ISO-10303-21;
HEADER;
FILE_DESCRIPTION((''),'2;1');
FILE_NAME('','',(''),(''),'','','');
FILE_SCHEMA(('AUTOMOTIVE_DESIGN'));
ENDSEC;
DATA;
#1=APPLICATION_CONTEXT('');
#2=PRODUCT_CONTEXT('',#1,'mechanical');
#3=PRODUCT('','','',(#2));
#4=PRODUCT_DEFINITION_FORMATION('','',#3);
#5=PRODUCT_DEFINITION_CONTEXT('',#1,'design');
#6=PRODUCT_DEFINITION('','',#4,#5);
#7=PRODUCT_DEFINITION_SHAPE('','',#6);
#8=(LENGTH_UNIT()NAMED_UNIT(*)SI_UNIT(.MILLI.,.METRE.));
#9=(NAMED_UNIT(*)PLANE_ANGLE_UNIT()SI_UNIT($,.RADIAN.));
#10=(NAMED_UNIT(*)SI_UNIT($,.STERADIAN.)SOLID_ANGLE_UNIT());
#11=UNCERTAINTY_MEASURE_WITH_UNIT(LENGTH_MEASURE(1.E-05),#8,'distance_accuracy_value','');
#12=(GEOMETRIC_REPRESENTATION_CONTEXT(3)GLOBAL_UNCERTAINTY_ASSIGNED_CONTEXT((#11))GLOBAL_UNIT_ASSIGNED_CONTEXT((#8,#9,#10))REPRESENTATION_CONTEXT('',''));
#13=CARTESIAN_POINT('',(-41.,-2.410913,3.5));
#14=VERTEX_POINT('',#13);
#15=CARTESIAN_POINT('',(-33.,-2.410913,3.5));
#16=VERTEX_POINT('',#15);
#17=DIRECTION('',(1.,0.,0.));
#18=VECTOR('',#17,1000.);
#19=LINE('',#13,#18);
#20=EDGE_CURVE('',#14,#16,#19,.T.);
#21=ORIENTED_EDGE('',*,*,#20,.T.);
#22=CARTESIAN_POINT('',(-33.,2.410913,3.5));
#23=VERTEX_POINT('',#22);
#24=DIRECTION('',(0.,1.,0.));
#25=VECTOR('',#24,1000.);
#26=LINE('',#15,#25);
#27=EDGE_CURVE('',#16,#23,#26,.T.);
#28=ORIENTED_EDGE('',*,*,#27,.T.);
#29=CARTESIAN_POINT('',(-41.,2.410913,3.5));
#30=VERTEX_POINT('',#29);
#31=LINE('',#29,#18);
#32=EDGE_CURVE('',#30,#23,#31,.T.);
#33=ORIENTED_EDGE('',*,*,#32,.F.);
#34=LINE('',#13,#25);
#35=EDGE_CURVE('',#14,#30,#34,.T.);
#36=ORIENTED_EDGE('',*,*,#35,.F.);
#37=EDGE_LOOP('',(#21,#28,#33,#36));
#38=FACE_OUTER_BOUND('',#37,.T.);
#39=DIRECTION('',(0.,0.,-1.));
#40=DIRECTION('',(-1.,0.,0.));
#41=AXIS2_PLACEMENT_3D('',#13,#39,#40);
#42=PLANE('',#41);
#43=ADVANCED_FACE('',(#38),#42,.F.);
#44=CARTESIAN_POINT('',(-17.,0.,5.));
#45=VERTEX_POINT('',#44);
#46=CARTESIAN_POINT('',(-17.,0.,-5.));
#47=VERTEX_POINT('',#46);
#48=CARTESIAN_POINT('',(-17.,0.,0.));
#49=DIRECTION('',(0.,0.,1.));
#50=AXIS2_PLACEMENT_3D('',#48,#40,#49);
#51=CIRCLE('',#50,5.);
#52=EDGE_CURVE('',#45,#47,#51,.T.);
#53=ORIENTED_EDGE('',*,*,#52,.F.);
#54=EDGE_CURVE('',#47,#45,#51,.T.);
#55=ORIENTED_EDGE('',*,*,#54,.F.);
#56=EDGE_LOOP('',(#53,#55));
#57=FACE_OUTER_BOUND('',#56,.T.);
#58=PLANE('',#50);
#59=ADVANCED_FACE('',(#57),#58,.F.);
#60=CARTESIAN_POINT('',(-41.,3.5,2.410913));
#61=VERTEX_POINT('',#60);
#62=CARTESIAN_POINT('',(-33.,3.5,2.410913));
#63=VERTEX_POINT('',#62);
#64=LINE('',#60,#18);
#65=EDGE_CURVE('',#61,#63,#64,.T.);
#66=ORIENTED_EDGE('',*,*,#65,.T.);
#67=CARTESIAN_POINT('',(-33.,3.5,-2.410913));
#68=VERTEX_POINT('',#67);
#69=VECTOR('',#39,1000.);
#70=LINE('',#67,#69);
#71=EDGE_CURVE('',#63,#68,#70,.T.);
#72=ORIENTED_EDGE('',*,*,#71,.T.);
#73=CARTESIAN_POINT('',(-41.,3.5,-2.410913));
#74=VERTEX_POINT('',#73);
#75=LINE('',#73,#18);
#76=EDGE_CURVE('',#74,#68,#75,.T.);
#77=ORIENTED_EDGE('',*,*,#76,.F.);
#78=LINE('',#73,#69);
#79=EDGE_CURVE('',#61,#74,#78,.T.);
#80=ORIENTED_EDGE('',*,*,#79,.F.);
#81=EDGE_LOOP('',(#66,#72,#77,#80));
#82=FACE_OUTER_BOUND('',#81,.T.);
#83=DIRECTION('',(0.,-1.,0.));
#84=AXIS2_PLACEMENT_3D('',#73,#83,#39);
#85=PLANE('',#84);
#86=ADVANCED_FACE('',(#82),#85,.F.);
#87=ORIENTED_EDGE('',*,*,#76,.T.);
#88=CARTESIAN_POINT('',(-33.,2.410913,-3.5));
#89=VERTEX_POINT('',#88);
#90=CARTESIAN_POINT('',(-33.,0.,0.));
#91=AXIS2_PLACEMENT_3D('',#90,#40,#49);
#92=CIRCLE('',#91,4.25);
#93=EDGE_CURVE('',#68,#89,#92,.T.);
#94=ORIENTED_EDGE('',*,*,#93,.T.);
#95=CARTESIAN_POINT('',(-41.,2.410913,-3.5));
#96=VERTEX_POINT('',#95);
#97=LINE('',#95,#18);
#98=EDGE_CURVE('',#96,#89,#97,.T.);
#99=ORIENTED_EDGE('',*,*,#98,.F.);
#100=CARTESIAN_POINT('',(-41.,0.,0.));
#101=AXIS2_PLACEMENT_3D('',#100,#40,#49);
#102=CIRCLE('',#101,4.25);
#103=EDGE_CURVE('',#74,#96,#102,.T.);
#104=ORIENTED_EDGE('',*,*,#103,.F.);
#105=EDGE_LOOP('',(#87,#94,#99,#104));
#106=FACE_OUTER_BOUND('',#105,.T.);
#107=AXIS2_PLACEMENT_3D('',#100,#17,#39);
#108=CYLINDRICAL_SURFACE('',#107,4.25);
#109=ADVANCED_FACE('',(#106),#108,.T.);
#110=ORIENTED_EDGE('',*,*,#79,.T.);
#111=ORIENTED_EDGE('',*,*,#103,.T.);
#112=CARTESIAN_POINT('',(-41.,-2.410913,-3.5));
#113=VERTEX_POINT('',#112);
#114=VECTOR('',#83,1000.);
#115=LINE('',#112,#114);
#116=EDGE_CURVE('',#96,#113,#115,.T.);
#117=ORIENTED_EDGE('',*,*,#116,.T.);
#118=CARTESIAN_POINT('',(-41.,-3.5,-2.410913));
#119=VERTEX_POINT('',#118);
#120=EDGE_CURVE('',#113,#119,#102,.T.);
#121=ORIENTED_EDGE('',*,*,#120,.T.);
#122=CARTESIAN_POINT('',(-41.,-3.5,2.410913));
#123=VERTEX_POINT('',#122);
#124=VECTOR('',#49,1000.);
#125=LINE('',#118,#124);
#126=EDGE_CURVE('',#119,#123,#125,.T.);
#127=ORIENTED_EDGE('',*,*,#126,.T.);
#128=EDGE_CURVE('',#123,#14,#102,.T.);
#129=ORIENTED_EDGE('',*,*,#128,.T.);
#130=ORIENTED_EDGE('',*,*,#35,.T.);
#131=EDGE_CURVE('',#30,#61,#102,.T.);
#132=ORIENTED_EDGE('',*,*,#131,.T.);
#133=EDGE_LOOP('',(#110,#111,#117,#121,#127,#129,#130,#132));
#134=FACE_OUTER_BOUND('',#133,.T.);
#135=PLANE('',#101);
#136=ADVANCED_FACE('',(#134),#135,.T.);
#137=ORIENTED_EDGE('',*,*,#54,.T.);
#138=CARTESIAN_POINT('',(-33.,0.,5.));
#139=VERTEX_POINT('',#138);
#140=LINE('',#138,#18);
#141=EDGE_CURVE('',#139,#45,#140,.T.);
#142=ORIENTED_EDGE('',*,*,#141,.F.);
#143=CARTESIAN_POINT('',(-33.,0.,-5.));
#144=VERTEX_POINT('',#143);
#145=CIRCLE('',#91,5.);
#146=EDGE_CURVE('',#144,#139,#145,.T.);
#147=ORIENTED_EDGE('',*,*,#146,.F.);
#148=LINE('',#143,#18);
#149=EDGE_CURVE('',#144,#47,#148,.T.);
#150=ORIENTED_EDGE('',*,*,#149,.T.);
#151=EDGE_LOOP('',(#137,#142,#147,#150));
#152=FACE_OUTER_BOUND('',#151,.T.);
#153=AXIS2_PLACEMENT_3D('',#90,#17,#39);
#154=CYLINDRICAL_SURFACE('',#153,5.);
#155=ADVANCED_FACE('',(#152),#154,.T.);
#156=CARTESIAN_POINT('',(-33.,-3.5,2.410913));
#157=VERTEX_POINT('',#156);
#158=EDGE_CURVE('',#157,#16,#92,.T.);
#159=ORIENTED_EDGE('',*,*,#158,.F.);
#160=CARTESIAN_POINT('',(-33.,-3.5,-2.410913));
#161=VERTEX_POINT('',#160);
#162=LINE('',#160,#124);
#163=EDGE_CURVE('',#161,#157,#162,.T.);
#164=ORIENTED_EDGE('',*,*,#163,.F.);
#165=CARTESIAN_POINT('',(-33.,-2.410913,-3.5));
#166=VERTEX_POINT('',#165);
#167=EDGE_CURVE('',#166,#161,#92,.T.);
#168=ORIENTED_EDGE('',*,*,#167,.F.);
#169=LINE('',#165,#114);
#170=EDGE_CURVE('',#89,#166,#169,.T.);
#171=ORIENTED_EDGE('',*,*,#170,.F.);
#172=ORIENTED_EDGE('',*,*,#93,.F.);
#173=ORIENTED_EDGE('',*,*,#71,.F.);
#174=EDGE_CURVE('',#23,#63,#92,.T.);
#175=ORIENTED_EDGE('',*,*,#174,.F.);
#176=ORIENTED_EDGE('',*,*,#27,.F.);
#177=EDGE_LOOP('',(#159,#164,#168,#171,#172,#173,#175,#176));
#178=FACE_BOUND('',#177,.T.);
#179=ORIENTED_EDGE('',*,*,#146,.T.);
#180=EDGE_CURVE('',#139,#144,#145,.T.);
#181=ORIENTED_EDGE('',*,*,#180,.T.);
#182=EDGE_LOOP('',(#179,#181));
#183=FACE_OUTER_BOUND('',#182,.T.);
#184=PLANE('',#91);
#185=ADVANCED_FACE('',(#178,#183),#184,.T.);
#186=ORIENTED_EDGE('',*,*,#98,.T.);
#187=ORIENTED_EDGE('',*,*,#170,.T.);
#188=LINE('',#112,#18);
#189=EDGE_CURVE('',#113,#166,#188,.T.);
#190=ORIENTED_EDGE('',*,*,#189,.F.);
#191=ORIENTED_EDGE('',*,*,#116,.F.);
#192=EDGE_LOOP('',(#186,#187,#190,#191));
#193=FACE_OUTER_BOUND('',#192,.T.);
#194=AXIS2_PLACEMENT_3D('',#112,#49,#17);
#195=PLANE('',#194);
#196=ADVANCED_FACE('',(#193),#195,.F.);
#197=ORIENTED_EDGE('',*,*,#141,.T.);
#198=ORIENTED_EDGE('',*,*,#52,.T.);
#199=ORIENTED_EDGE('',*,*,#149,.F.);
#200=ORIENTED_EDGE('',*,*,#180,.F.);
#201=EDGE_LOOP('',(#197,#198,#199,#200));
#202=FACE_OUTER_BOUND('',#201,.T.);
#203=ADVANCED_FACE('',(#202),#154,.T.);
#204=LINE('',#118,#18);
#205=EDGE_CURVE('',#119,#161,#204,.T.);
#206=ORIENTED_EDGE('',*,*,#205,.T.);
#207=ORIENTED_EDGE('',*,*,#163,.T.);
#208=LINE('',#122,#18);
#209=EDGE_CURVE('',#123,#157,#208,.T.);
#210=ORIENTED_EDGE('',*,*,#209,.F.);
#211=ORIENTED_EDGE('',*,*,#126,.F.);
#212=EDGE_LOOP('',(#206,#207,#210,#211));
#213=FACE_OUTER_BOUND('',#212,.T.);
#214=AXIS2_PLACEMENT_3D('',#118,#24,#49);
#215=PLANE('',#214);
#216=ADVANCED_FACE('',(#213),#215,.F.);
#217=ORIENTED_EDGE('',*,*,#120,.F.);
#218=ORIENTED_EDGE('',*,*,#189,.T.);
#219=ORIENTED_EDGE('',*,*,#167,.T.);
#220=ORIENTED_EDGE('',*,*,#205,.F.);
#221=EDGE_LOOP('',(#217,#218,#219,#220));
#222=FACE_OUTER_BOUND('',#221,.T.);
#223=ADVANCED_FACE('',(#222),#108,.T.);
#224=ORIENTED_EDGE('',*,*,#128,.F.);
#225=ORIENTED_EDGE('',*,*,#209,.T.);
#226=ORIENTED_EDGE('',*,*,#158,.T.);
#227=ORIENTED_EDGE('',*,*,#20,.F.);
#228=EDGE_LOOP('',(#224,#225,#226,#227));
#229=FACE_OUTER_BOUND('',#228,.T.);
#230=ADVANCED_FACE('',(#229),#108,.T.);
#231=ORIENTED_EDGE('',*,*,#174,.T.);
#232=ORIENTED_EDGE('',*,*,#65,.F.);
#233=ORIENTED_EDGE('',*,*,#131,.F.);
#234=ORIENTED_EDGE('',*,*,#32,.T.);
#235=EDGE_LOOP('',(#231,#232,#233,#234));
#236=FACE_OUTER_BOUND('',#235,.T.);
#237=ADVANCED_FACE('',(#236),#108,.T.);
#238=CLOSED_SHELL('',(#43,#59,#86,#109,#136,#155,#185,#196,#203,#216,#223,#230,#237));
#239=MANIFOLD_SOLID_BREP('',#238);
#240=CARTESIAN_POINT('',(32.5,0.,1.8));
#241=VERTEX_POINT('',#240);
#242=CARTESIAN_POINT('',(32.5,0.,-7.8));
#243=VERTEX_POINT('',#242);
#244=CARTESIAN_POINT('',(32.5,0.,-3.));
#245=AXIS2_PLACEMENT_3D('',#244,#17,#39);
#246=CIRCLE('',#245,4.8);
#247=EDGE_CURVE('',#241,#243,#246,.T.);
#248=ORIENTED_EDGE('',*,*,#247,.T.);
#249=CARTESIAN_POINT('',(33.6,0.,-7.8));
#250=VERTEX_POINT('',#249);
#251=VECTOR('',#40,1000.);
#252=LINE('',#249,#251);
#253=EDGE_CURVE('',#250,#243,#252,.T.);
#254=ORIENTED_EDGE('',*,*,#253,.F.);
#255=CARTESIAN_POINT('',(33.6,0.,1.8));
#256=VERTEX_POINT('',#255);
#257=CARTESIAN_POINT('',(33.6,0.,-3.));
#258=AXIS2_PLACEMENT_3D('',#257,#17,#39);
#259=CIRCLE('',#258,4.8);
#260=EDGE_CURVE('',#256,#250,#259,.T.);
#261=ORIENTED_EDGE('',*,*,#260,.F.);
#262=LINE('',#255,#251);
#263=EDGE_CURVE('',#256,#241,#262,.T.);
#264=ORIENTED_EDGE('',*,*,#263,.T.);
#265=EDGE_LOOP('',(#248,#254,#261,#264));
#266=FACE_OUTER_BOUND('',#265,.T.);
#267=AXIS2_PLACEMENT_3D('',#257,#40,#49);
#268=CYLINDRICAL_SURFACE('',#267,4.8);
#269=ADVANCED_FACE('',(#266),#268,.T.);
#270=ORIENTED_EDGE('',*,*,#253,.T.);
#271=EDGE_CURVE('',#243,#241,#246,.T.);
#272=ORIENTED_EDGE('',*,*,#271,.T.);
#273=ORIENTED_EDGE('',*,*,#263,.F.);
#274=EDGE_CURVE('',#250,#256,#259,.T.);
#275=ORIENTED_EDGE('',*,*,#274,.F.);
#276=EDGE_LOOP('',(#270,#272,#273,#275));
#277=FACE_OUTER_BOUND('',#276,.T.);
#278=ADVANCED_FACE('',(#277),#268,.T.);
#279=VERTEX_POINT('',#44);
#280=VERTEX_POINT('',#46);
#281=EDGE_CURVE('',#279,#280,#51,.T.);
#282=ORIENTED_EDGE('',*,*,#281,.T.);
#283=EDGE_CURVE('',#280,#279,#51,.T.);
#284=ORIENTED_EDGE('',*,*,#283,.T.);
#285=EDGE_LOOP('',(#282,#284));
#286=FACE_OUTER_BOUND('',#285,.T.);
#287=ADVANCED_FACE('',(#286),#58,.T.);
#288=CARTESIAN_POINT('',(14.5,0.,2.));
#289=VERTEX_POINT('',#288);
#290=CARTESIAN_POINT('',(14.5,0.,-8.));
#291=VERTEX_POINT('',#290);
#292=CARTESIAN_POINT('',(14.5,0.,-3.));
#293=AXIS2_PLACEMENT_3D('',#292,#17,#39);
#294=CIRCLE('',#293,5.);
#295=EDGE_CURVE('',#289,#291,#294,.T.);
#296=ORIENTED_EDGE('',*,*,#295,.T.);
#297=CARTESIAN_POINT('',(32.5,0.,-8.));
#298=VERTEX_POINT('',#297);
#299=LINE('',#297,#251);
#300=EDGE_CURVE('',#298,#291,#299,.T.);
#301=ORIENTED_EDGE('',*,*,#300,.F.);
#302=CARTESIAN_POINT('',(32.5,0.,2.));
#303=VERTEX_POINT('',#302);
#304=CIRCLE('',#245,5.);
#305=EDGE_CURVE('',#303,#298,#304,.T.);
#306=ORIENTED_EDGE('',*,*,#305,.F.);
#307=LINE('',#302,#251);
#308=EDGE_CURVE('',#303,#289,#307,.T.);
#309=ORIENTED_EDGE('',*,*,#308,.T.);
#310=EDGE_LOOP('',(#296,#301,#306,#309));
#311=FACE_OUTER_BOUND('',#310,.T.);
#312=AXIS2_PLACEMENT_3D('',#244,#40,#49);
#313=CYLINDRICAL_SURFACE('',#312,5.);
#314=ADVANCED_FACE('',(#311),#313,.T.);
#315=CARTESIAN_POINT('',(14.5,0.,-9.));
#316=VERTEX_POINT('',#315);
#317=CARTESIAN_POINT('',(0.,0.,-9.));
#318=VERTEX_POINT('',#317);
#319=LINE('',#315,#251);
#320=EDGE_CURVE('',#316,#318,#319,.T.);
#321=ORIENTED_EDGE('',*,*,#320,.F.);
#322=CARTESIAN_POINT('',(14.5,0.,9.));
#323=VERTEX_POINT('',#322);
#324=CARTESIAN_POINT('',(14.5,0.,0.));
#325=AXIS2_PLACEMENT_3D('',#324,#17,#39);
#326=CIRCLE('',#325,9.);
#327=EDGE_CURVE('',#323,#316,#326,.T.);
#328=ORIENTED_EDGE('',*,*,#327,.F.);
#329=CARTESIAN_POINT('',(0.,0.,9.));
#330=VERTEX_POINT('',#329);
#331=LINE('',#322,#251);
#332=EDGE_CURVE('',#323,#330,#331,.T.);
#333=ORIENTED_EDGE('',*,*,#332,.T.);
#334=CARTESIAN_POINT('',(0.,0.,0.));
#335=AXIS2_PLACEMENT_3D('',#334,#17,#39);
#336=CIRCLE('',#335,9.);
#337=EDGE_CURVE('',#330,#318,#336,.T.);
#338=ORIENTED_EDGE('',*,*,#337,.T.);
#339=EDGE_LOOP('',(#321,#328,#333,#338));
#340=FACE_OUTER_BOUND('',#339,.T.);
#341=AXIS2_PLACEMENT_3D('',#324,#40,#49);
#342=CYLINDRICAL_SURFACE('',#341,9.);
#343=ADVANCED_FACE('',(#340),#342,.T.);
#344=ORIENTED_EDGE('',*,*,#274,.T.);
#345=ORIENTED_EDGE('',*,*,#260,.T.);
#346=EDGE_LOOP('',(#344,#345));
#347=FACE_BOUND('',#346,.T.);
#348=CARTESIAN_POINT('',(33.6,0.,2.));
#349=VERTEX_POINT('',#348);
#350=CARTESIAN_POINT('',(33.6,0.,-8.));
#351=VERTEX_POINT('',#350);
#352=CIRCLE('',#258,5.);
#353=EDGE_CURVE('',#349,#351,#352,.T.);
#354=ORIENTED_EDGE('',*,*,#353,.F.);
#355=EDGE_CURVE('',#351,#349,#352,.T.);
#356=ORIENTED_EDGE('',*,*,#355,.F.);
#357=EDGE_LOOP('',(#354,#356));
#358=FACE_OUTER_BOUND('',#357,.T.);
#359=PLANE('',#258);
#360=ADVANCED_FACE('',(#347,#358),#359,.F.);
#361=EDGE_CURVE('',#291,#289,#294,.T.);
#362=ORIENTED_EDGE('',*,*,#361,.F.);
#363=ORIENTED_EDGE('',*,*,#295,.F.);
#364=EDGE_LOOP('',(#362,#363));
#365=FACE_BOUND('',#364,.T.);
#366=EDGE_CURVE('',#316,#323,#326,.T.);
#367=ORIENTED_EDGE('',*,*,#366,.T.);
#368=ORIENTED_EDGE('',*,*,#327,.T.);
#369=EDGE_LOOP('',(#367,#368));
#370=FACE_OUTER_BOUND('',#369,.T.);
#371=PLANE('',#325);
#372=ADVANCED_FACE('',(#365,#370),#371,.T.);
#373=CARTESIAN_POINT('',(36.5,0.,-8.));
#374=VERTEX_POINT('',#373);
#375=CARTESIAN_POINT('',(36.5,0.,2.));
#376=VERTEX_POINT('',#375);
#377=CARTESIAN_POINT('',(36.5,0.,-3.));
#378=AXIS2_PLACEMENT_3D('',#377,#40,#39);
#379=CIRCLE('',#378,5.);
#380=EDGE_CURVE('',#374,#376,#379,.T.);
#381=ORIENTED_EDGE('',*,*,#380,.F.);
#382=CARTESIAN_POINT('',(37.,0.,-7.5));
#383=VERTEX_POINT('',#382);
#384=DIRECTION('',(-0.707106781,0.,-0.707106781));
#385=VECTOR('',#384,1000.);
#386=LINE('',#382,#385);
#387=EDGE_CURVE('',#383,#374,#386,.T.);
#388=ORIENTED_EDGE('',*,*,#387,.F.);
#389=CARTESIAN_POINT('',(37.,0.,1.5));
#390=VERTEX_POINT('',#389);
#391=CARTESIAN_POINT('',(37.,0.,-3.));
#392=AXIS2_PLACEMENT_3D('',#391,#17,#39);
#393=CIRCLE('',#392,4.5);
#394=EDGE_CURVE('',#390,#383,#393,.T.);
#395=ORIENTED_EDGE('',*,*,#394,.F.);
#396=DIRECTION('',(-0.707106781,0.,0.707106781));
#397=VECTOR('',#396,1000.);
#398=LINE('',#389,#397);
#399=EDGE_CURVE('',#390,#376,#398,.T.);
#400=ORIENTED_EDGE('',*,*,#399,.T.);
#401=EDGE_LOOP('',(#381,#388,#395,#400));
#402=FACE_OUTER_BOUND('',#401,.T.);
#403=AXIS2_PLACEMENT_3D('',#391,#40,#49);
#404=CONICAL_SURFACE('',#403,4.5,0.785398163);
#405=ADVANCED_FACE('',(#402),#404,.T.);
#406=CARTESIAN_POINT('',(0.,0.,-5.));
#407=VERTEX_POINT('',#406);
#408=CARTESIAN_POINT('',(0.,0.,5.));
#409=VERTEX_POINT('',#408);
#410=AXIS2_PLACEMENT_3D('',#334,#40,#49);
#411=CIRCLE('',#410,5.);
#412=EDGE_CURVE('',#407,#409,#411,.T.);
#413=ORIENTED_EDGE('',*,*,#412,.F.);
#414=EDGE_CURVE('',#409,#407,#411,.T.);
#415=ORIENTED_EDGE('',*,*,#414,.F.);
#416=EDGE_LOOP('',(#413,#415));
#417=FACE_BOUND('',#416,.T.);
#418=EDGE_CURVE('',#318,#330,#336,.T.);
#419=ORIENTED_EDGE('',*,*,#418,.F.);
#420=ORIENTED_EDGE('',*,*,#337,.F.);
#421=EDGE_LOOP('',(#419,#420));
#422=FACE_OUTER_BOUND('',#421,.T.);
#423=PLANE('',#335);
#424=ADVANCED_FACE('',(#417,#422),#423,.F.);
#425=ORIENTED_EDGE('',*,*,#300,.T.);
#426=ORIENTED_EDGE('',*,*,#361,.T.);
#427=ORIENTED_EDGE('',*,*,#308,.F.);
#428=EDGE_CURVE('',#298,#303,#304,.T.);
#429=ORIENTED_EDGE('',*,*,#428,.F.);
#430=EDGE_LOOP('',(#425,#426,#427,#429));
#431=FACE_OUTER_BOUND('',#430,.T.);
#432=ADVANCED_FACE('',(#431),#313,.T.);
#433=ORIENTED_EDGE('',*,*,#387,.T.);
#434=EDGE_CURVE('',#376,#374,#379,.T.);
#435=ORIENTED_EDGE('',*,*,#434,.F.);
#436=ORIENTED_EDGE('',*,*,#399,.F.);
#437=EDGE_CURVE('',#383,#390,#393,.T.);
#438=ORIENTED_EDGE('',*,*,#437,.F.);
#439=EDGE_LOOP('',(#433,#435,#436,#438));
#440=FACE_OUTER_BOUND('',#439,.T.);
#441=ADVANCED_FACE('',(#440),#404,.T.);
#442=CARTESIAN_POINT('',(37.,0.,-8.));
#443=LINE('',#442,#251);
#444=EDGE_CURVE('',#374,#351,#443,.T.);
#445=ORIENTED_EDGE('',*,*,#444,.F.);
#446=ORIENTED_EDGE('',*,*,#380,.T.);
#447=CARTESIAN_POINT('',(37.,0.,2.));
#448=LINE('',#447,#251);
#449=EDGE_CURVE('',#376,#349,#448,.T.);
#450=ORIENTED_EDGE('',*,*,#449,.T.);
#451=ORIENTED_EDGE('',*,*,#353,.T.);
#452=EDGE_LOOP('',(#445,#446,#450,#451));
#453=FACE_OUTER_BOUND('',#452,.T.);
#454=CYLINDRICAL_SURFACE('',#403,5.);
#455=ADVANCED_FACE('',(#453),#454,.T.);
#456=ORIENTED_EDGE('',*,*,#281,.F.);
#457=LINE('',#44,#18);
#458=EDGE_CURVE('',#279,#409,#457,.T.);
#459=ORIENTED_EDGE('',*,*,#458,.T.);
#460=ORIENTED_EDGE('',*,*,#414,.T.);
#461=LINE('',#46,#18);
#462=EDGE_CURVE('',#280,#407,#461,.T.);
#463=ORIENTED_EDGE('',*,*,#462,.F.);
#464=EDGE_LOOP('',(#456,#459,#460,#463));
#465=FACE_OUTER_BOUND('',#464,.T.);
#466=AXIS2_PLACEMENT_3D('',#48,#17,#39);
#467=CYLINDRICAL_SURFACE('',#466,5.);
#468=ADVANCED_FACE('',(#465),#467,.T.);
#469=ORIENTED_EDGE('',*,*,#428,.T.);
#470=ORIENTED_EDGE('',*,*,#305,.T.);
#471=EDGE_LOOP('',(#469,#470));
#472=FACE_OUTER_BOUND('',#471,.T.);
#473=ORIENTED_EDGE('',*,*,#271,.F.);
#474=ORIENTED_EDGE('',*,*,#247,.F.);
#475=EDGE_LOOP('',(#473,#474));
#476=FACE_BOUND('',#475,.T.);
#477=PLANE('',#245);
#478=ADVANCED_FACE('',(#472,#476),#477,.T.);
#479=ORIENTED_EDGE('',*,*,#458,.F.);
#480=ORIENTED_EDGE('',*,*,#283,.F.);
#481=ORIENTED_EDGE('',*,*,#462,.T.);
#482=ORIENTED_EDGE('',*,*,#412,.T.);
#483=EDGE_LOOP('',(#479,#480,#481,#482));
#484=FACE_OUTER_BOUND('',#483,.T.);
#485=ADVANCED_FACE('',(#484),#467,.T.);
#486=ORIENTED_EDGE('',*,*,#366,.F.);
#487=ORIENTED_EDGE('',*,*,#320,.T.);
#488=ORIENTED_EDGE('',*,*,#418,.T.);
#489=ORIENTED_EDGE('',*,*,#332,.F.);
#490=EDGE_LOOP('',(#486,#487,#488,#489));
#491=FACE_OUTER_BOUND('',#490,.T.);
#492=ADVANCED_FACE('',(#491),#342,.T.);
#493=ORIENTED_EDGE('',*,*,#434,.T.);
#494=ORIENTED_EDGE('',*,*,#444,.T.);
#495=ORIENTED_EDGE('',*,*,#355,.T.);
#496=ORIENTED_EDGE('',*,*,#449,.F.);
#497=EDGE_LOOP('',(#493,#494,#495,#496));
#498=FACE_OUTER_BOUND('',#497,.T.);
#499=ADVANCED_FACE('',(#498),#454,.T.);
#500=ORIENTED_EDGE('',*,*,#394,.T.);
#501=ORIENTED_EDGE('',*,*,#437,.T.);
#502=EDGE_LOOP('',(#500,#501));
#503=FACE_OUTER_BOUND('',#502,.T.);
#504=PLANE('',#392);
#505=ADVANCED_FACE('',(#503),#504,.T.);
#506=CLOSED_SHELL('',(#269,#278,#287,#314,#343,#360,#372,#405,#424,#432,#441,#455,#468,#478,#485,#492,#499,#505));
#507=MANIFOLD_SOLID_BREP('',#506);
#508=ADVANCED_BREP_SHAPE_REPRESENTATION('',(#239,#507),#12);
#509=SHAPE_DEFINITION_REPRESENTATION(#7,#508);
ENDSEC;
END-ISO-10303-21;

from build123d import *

# Parameters (mm, degrees)
SKETCH_2_R      = 9
EXTRUDE_1_DEPTH = 14.5
SKETCH_3_R      = 5
EXTRUDE_2_DEPTH = 18
SKETCH_4_R      = 4.8
EXTRUDE_3_DEPTH = 1.1
SKETCH_5_R      = 5
EXTRUDE_4_DEPTH = 3.4
CHAMFER_1_SIZE  = 0.5
SKETCH_6_R      = 5
EXTRUDE_5_DEPTH = 17
SKETCH_7_R      = 5
EXTRUDE_6_DEPTH = 16
EXTRUDE_7_DEPTH = 8


with BuildPart() as part:
    # 草图2 → 凸台-拉伸1 (new body)
    with BuildSketch(Plane(origin=(0, 0, 0), x_dir=(0, 0, -1), z_dir=(1, 0, 0))):
        with Locations(Location((0, 0, 0), (0, 0, 180))):
            Circle(SKETCH_2_R)
    extrude(amount=EXTRUDE_1_DEPTH)

    # 草图3 → 凸台-拉伸2 (add)
    with BuildSketch(Plane(origin=(14.5, 0, 0), x_dir=(0, 0, -1), z_dir=(1, 0, 0))):
        with Locations((3, 0)):
            Circle(SKETCH_3_R)
    extrude(amount=EXTRUDE_2_DEPTH)

    # 草图4 → 凸台-拉伸3 (add)
    with BuildSketch(Plane(origin=(32.5, 0, 0), x_dir=(0, 0, -1), z_dir=(1, 0, 0))):
        with Locations((3, 0)):
            Circle(SKETCH_4_R)
    extrude(amount=EXTRUDE_3_DEPTH)

    # 草图5 → 凸台-拉伸4 (add)
    with BuildSketch(Plane(origin=(33.6, 0, 0), x_dir=(0, 0, -1), z_dir=(1, 0, 0))):
        with Locations((3, 0)):
            Circle(SKETCH_5_R)
    extrude(amount=EXTRUDE_4_DEPTH)

    # 倒角1
    chamfer_1_edges = [part.edges().sort_by_distance(p)[0] for p in [
        (37, 0, 2),
    ]]
    chamfer(chamfer_1_edges, length=CHAMFER_1_SIZE)

    # 草图6 → 凸台-拉伸5 (add)
    with BuildSketch(Plane.ZY):
        Circle(SKETCH_6_R)
    extrude(amount=EXTRUDE_5_DEPTH)


with BuildPart() as body_2:
    # 草图7 → 凸台-拉伸6 (new body)
    with BuildSketch(Plane.ZY.offset(17)):
        Circle(SKETCH_7_R)
    extrude(amount=EXTRUDE_6_DEPTH)

    # 草图8 → 凸台-拉伸7 (add)
    with BuildSketch(Plane.ZY.offset(33)):
        with BuildLine():
            Line((-2.41091269, -3.5), (2.41091269, -3.5))
            ThreePointArc((2.41091269, -3.5), (3.00520382, -3.00520382), (3.5, -2.41091269))
            Line((3.5, -2.41091269), (3.5, 2.41091269))
            ThreePointArc((3.5, 2.41091269), (3.00520382, 3.00520382), (2.41091269, 3.5))
            Line((2.41091269, 3.5), (-2.41091269, 3.5))
            ThreePointArc((-2.41091269, 3.5), (-3.00520382, 3.00520382), (-3.5, 2.41091269))
            Line((-3.5, 2.41091269), (-3.5, -2.41091269))
            ThreePointArc((-3.5, -2.41091269), (-3.00520382, -3.00520382), (-2.41091269, -3.5))
        make_face()
    extrude(amount=EXTRUDE_7_DEPTH)


solid = Compound([part.part, body_2.part])
